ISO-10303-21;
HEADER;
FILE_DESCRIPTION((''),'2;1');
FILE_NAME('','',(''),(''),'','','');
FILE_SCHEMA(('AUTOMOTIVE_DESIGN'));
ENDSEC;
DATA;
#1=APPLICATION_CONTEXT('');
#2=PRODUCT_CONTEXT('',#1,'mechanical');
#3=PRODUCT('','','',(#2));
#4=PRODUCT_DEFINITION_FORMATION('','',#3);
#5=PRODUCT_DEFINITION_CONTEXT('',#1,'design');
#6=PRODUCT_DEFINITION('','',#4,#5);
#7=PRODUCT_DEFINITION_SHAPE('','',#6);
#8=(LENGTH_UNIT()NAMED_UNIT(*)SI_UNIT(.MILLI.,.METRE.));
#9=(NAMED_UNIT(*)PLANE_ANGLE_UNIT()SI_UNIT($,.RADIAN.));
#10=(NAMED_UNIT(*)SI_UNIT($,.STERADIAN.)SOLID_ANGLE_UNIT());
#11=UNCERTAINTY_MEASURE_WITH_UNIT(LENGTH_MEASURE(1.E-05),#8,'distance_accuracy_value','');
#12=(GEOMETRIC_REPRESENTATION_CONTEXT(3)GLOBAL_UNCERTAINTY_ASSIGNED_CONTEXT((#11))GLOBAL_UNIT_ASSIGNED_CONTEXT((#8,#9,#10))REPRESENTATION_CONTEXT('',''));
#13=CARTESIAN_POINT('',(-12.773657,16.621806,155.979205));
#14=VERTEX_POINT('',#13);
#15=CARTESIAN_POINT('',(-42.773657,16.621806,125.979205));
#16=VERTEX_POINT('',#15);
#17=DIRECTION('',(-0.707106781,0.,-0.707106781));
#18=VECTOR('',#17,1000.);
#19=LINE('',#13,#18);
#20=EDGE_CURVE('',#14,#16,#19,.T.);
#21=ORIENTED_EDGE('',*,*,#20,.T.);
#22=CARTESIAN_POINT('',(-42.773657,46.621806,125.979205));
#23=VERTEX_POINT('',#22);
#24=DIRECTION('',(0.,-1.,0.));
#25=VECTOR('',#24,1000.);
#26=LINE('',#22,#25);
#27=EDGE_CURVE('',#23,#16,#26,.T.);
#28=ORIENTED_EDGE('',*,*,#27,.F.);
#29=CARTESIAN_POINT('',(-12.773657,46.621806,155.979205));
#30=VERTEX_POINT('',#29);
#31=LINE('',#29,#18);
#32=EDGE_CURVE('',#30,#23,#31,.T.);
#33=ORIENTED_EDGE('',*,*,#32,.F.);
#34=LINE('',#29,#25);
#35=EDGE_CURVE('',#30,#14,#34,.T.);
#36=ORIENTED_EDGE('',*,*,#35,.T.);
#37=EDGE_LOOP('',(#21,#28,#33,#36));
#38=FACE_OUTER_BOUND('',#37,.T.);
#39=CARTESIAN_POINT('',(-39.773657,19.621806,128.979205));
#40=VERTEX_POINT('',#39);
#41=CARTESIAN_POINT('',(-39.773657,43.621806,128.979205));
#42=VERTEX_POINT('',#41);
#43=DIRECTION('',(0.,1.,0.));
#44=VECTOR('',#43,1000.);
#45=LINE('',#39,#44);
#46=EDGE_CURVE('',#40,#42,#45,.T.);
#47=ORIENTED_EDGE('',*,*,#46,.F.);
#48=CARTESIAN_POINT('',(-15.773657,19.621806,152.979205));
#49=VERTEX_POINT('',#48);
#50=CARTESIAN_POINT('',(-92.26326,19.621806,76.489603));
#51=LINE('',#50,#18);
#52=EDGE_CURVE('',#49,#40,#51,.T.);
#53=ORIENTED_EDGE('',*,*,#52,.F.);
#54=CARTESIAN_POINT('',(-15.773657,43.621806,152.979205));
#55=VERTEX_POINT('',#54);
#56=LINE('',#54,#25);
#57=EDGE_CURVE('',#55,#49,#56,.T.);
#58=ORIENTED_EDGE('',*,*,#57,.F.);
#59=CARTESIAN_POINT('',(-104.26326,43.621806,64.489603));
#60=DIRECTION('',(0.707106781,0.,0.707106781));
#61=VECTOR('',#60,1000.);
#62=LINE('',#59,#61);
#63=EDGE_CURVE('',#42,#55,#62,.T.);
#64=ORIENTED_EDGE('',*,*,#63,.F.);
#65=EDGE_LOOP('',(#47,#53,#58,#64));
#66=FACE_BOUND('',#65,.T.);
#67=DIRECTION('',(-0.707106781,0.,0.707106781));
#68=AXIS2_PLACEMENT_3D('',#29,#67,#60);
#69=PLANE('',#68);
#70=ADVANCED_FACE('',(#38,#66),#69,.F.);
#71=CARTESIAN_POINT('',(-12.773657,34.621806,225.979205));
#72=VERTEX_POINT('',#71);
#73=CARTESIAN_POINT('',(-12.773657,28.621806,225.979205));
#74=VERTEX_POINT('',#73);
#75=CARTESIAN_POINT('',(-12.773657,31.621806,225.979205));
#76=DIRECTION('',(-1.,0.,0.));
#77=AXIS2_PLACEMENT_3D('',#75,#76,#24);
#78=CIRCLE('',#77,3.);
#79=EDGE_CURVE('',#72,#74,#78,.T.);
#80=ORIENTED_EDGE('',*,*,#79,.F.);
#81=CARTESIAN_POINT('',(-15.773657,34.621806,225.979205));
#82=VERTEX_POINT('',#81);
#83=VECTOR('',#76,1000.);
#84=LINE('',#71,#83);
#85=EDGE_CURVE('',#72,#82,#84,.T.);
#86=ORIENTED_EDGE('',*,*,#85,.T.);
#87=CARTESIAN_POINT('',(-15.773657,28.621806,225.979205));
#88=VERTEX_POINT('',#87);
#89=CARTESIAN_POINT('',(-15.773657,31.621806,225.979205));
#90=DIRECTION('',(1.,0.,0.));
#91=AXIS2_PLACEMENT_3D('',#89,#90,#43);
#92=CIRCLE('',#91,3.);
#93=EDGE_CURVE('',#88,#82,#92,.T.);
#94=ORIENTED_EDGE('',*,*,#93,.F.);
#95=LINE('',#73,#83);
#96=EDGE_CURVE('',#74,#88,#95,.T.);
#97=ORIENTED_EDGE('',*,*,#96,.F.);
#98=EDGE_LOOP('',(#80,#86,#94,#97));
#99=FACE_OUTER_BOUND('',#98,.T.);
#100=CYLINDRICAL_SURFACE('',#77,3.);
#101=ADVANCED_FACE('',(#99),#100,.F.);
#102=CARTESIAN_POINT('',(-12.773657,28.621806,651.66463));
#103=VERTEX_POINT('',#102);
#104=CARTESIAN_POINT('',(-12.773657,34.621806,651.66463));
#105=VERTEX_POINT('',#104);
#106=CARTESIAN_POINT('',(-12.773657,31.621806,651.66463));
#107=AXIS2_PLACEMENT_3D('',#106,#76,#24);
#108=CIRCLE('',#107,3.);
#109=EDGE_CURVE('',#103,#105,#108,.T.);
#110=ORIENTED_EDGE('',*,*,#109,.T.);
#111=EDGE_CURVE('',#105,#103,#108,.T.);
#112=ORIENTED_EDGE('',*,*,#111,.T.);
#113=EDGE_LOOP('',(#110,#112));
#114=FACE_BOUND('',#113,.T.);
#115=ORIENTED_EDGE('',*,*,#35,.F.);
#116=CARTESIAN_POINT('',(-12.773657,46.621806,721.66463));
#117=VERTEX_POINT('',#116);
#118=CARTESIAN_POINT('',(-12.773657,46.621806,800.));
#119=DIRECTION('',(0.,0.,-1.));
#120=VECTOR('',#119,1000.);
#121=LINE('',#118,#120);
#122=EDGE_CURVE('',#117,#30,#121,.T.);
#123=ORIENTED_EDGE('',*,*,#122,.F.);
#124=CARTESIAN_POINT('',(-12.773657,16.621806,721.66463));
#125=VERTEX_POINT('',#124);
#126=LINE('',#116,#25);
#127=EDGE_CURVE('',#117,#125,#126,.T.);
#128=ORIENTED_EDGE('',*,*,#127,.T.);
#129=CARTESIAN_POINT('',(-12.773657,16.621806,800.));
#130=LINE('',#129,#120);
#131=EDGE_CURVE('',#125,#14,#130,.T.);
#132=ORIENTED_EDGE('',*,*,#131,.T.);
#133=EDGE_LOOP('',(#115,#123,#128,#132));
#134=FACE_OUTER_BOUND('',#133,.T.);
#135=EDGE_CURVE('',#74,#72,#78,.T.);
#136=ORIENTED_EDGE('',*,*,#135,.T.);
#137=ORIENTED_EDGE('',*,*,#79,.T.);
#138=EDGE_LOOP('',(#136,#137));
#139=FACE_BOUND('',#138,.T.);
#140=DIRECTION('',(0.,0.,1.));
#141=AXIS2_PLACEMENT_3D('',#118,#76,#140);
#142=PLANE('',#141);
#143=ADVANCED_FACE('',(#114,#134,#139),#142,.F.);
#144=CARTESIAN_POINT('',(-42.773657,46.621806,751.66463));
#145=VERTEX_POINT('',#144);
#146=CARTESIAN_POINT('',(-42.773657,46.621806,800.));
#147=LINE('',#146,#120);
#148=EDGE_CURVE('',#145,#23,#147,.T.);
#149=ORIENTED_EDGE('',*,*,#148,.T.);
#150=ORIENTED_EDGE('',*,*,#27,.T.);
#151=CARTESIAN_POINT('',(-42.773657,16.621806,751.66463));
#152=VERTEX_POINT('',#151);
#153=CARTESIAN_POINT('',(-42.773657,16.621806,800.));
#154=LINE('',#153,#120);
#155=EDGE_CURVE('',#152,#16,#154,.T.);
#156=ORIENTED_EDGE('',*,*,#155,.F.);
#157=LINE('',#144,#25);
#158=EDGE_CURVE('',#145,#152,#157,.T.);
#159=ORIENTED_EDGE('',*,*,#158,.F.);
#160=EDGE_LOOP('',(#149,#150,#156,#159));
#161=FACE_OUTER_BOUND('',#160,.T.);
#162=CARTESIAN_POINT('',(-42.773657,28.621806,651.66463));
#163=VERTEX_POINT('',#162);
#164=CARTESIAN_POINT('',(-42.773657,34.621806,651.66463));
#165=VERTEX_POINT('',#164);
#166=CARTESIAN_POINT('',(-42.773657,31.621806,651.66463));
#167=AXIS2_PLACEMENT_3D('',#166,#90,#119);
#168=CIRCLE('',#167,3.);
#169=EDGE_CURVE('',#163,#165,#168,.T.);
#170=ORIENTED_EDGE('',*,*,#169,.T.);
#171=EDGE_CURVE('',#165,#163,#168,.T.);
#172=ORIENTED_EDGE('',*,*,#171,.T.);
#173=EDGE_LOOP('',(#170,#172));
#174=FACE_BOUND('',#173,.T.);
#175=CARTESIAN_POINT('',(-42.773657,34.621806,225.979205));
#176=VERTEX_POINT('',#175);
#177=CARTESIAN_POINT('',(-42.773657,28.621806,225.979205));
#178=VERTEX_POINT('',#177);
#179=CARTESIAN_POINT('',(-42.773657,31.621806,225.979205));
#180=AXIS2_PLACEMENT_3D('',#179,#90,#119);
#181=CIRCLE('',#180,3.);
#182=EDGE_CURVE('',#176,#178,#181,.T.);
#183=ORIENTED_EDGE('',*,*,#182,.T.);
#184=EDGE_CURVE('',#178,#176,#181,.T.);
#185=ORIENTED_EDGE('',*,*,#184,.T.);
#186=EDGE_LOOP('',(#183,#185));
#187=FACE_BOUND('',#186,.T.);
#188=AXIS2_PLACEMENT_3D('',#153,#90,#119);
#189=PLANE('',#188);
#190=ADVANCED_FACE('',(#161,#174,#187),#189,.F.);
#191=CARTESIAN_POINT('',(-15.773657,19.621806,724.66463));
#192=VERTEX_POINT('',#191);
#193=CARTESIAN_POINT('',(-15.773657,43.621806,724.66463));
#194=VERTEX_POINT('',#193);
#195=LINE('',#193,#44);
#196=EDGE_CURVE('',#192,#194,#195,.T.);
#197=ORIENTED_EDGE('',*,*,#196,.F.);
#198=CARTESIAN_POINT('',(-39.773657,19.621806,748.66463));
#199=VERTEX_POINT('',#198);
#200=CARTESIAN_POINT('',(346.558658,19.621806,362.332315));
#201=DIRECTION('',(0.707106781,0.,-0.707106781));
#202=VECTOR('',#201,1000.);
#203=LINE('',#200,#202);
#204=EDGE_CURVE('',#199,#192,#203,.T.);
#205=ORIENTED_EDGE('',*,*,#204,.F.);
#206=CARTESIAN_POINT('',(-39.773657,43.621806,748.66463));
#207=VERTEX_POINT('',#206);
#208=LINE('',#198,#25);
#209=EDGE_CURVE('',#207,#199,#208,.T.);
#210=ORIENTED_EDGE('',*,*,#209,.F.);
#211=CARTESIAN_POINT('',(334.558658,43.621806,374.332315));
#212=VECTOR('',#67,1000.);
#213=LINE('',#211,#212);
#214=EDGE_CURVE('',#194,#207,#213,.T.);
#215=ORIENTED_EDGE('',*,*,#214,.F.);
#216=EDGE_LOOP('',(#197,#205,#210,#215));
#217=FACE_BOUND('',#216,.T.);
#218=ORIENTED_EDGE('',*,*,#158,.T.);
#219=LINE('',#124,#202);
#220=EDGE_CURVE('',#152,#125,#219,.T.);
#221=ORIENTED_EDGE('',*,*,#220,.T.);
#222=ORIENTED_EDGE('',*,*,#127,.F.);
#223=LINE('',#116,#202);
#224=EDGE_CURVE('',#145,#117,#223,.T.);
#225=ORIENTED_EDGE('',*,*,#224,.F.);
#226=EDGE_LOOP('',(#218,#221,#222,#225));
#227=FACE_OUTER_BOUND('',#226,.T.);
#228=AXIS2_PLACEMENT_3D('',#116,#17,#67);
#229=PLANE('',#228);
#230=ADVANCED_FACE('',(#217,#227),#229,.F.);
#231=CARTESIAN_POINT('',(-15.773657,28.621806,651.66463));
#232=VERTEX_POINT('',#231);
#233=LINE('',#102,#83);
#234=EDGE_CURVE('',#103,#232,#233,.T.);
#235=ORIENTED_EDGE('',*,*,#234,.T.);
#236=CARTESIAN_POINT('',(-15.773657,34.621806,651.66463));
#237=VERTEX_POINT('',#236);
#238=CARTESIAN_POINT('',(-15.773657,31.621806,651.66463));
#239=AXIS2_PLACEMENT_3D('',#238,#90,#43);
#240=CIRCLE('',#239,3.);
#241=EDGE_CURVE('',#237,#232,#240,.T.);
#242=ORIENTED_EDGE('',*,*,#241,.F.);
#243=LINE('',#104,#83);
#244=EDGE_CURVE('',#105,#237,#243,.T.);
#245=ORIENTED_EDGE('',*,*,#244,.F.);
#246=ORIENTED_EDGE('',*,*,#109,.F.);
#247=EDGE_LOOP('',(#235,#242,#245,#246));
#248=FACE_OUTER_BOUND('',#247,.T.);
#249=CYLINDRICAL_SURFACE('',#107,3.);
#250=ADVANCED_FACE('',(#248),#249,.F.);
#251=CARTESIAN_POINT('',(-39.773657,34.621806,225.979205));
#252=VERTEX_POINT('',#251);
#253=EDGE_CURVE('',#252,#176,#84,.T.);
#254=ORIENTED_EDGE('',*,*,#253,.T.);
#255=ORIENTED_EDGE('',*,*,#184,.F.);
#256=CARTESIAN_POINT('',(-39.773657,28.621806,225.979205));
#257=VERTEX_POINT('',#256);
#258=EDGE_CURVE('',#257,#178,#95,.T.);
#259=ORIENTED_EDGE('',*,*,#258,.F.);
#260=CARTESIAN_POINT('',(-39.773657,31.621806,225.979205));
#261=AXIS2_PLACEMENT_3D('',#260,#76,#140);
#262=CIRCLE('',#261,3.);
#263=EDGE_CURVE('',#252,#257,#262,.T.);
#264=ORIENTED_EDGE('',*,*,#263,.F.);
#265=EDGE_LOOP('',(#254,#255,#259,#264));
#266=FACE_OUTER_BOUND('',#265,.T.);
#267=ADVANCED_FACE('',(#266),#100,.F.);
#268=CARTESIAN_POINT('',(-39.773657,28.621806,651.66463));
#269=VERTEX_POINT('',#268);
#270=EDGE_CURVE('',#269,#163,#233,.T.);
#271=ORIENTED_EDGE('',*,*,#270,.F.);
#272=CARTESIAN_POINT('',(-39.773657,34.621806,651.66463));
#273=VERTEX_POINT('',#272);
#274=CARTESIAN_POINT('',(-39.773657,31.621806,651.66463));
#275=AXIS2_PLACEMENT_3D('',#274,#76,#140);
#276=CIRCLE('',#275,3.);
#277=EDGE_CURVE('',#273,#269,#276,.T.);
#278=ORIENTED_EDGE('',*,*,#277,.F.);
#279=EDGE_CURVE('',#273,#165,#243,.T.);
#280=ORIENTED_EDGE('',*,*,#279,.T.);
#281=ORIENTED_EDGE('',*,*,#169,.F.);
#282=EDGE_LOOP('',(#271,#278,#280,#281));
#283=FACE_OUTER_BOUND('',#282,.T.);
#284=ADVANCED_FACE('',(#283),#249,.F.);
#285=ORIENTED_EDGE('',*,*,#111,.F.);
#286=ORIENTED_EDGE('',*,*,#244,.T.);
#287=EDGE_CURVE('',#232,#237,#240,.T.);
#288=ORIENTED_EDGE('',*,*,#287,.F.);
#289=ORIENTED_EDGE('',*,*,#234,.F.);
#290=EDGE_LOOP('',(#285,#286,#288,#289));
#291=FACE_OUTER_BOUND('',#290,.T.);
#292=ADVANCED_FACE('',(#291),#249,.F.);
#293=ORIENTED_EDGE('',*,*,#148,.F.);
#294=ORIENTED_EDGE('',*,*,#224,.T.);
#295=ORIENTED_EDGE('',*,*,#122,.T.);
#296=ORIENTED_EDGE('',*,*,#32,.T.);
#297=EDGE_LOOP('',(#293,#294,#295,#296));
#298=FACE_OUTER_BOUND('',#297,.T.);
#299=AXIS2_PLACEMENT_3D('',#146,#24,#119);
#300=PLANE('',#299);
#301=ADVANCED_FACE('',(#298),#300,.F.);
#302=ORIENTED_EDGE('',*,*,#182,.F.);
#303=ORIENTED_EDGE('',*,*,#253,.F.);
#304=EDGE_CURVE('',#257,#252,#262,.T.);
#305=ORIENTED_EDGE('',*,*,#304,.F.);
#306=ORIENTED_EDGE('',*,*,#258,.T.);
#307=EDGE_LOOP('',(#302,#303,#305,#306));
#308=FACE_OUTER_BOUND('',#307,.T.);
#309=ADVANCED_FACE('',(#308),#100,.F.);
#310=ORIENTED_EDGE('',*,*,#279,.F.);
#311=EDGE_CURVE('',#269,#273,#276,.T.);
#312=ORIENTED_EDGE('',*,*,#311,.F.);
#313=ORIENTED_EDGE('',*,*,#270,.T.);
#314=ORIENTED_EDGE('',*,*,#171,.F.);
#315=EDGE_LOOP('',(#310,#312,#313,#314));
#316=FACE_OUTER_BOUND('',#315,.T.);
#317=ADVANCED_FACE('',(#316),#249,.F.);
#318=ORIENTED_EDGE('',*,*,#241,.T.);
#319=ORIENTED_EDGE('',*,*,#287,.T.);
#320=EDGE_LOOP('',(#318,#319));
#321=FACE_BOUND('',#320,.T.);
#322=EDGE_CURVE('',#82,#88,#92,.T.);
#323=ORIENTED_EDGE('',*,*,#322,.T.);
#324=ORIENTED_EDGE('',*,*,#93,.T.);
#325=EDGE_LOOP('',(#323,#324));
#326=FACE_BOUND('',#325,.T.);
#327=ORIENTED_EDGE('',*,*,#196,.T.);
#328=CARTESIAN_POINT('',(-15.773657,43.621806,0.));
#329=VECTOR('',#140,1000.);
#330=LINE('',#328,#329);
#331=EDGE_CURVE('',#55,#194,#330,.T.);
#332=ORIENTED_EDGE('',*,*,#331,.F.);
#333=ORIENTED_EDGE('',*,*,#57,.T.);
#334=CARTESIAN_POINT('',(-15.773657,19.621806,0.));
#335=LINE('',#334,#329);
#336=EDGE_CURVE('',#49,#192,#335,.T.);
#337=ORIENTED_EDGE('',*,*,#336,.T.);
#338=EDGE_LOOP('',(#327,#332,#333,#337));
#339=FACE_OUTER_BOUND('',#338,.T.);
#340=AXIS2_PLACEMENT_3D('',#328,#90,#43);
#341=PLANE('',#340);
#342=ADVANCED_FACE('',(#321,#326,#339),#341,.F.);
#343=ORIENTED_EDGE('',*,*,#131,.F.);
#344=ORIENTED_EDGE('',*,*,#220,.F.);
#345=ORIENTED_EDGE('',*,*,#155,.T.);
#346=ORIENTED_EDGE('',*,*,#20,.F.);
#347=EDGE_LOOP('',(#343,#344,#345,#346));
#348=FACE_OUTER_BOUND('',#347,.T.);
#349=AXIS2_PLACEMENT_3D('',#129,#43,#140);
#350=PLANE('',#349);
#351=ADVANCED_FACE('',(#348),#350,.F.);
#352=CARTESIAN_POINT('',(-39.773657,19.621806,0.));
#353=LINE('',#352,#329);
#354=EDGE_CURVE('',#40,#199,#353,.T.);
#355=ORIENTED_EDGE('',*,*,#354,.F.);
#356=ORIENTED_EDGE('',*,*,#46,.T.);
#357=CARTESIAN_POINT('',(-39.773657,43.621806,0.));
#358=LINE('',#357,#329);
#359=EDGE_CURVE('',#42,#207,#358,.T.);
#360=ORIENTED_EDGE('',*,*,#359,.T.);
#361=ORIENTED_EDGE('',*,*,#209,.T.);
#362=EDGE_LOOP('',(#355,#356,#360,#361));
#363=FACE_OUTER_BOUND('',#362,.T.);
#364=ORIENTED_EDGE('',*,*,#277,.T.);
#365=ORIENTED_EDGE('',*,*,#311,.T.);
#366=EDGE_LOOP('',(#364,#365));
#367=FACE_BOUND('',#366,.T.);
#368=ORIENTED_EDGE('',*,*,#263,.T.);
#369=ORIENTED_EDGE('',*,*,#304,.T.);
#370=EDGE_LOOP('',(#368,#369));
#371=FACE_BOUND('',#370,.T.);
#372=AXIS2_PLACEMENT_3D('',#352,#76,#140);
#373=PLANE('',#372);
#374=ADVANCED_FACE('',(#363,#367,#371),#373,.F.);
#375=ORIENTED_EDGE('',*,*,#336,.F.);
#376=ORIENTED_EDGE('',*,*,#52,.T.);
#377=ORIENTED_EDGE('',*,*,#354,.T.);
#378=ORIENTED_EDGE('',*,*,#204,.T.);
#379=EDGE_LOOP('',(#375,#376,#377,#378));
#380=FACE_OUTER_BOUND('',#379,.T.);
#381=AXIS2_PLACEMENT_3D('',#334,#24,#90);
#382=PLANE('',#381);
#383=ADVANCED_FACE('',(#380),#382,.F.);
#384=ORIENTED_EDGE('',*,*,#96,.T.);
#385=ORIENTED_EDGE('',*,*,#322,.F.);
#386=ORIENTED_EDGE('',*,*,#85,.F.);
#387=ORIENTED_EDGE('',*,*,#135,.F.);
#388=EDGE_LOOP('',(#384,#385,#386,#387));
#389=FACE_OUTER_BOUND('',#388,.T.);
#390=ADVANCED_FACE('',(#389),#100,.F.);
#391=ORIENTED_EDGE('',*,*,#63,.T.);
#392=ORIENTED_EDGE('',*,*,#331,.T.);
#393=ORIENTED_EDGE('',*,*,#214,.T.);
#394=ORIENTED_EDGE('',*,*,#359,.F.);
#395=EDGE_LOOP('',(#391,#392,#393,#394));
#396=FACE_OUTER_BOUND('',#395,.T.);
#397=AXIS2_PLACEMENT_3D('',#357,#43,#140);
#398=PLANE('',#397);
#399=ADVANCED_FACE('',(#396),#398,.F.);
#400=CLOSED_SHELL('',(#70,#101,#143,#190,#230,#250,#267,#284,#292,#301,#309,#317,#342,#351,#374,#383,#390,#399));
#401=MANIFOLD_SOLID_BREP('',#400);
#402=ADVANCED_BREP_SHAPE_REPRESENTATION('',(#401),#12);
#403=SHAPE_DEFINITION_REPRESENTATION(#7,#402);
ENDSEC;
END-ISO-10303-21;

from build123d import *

# Parameters (mm, degrees)
SKETCH1_W           = 30
SKETCH1_H           = 30
BOSS_EXTRUDE1_DEPTH = 800
SKETCH2_W           = 24
SKETCH2_H           = 24
CUT_EXTRUDE1_DEPTH  = 800
CUT_EXTRUDE2_DEPTH  = 802.704175948
SKETCH4_R           = 3
CUT_EXTRUDE3_DEPTH  = 754.969037173


with BuildPart() as part:
    # Sketch1 → Boss-Extrude1 (new body)
    with BuildSketch(Plane.XY):
        with Locations((-27.773656986, 31.621806058)):
            Rectangle(SKETCH1_W, SKETCH1_H)
    extrude(amount=BOSS_EXTRUDE1_DEPTH)

    # Sketch2 → Cut-Extrude1 (cut)
    with BuildSketch(Plane.XY.offset(800)):
        with Locations((-27.773656986, 31.621806058)):
            Rectangle(SKETCH2_W, SKETCH2_H)
    extrude(amount=-CUT_EXTRUDE1_DEPTH, mode=Mode.SUBTRACT)

    # Sketch3 → Cut-Extrude2 (cut, through all)
    with BuildSketch(Plane(origin=(0, 16.621806058, 0), x_dir=(-1, 0, 0), z_dir=(0, -1, 0))):
        Polygon((12.773656986, -721.664630148), (42.773656986, -751.664630148), (42.773656986, -800), (12.773656986, -800), align=None)
        Polygon((12.773656986, -155.979205198), (42.773656986, -125.979205198), (42.773656986, 0), (12.773656986, 0), align=None)
    extrude(amount=-CUT_EXTRUDE2_DEPTH, mode=Mode.SUBTRACT)

    # Sketch4 → Cut-Extrude3 (cut, through all)
    with BuildSketch(Plane.ZY.offset(48.773656986)):
        with Locations(Location((225.979205198, 31.621806058, 0), (0, 0, 270))):
            Circle(SKETCH4_R)
        with Locations((225.979205198, 841.621806058)):
            Circle(SKETCH4_R)
        with Locations((651.664630148, 841.621806058)):
            Circle(SKETCH4_R)
        with Locations(Location((651.664630148, 31.621806058, 0), (0, 0, 269.999999999))):
            Circle(SKETCH4_R)
    extrude(amount=-CUT_EXTRUDE3_DEPTH, mode=Mode.SUBTRACT)


solid = part.part
